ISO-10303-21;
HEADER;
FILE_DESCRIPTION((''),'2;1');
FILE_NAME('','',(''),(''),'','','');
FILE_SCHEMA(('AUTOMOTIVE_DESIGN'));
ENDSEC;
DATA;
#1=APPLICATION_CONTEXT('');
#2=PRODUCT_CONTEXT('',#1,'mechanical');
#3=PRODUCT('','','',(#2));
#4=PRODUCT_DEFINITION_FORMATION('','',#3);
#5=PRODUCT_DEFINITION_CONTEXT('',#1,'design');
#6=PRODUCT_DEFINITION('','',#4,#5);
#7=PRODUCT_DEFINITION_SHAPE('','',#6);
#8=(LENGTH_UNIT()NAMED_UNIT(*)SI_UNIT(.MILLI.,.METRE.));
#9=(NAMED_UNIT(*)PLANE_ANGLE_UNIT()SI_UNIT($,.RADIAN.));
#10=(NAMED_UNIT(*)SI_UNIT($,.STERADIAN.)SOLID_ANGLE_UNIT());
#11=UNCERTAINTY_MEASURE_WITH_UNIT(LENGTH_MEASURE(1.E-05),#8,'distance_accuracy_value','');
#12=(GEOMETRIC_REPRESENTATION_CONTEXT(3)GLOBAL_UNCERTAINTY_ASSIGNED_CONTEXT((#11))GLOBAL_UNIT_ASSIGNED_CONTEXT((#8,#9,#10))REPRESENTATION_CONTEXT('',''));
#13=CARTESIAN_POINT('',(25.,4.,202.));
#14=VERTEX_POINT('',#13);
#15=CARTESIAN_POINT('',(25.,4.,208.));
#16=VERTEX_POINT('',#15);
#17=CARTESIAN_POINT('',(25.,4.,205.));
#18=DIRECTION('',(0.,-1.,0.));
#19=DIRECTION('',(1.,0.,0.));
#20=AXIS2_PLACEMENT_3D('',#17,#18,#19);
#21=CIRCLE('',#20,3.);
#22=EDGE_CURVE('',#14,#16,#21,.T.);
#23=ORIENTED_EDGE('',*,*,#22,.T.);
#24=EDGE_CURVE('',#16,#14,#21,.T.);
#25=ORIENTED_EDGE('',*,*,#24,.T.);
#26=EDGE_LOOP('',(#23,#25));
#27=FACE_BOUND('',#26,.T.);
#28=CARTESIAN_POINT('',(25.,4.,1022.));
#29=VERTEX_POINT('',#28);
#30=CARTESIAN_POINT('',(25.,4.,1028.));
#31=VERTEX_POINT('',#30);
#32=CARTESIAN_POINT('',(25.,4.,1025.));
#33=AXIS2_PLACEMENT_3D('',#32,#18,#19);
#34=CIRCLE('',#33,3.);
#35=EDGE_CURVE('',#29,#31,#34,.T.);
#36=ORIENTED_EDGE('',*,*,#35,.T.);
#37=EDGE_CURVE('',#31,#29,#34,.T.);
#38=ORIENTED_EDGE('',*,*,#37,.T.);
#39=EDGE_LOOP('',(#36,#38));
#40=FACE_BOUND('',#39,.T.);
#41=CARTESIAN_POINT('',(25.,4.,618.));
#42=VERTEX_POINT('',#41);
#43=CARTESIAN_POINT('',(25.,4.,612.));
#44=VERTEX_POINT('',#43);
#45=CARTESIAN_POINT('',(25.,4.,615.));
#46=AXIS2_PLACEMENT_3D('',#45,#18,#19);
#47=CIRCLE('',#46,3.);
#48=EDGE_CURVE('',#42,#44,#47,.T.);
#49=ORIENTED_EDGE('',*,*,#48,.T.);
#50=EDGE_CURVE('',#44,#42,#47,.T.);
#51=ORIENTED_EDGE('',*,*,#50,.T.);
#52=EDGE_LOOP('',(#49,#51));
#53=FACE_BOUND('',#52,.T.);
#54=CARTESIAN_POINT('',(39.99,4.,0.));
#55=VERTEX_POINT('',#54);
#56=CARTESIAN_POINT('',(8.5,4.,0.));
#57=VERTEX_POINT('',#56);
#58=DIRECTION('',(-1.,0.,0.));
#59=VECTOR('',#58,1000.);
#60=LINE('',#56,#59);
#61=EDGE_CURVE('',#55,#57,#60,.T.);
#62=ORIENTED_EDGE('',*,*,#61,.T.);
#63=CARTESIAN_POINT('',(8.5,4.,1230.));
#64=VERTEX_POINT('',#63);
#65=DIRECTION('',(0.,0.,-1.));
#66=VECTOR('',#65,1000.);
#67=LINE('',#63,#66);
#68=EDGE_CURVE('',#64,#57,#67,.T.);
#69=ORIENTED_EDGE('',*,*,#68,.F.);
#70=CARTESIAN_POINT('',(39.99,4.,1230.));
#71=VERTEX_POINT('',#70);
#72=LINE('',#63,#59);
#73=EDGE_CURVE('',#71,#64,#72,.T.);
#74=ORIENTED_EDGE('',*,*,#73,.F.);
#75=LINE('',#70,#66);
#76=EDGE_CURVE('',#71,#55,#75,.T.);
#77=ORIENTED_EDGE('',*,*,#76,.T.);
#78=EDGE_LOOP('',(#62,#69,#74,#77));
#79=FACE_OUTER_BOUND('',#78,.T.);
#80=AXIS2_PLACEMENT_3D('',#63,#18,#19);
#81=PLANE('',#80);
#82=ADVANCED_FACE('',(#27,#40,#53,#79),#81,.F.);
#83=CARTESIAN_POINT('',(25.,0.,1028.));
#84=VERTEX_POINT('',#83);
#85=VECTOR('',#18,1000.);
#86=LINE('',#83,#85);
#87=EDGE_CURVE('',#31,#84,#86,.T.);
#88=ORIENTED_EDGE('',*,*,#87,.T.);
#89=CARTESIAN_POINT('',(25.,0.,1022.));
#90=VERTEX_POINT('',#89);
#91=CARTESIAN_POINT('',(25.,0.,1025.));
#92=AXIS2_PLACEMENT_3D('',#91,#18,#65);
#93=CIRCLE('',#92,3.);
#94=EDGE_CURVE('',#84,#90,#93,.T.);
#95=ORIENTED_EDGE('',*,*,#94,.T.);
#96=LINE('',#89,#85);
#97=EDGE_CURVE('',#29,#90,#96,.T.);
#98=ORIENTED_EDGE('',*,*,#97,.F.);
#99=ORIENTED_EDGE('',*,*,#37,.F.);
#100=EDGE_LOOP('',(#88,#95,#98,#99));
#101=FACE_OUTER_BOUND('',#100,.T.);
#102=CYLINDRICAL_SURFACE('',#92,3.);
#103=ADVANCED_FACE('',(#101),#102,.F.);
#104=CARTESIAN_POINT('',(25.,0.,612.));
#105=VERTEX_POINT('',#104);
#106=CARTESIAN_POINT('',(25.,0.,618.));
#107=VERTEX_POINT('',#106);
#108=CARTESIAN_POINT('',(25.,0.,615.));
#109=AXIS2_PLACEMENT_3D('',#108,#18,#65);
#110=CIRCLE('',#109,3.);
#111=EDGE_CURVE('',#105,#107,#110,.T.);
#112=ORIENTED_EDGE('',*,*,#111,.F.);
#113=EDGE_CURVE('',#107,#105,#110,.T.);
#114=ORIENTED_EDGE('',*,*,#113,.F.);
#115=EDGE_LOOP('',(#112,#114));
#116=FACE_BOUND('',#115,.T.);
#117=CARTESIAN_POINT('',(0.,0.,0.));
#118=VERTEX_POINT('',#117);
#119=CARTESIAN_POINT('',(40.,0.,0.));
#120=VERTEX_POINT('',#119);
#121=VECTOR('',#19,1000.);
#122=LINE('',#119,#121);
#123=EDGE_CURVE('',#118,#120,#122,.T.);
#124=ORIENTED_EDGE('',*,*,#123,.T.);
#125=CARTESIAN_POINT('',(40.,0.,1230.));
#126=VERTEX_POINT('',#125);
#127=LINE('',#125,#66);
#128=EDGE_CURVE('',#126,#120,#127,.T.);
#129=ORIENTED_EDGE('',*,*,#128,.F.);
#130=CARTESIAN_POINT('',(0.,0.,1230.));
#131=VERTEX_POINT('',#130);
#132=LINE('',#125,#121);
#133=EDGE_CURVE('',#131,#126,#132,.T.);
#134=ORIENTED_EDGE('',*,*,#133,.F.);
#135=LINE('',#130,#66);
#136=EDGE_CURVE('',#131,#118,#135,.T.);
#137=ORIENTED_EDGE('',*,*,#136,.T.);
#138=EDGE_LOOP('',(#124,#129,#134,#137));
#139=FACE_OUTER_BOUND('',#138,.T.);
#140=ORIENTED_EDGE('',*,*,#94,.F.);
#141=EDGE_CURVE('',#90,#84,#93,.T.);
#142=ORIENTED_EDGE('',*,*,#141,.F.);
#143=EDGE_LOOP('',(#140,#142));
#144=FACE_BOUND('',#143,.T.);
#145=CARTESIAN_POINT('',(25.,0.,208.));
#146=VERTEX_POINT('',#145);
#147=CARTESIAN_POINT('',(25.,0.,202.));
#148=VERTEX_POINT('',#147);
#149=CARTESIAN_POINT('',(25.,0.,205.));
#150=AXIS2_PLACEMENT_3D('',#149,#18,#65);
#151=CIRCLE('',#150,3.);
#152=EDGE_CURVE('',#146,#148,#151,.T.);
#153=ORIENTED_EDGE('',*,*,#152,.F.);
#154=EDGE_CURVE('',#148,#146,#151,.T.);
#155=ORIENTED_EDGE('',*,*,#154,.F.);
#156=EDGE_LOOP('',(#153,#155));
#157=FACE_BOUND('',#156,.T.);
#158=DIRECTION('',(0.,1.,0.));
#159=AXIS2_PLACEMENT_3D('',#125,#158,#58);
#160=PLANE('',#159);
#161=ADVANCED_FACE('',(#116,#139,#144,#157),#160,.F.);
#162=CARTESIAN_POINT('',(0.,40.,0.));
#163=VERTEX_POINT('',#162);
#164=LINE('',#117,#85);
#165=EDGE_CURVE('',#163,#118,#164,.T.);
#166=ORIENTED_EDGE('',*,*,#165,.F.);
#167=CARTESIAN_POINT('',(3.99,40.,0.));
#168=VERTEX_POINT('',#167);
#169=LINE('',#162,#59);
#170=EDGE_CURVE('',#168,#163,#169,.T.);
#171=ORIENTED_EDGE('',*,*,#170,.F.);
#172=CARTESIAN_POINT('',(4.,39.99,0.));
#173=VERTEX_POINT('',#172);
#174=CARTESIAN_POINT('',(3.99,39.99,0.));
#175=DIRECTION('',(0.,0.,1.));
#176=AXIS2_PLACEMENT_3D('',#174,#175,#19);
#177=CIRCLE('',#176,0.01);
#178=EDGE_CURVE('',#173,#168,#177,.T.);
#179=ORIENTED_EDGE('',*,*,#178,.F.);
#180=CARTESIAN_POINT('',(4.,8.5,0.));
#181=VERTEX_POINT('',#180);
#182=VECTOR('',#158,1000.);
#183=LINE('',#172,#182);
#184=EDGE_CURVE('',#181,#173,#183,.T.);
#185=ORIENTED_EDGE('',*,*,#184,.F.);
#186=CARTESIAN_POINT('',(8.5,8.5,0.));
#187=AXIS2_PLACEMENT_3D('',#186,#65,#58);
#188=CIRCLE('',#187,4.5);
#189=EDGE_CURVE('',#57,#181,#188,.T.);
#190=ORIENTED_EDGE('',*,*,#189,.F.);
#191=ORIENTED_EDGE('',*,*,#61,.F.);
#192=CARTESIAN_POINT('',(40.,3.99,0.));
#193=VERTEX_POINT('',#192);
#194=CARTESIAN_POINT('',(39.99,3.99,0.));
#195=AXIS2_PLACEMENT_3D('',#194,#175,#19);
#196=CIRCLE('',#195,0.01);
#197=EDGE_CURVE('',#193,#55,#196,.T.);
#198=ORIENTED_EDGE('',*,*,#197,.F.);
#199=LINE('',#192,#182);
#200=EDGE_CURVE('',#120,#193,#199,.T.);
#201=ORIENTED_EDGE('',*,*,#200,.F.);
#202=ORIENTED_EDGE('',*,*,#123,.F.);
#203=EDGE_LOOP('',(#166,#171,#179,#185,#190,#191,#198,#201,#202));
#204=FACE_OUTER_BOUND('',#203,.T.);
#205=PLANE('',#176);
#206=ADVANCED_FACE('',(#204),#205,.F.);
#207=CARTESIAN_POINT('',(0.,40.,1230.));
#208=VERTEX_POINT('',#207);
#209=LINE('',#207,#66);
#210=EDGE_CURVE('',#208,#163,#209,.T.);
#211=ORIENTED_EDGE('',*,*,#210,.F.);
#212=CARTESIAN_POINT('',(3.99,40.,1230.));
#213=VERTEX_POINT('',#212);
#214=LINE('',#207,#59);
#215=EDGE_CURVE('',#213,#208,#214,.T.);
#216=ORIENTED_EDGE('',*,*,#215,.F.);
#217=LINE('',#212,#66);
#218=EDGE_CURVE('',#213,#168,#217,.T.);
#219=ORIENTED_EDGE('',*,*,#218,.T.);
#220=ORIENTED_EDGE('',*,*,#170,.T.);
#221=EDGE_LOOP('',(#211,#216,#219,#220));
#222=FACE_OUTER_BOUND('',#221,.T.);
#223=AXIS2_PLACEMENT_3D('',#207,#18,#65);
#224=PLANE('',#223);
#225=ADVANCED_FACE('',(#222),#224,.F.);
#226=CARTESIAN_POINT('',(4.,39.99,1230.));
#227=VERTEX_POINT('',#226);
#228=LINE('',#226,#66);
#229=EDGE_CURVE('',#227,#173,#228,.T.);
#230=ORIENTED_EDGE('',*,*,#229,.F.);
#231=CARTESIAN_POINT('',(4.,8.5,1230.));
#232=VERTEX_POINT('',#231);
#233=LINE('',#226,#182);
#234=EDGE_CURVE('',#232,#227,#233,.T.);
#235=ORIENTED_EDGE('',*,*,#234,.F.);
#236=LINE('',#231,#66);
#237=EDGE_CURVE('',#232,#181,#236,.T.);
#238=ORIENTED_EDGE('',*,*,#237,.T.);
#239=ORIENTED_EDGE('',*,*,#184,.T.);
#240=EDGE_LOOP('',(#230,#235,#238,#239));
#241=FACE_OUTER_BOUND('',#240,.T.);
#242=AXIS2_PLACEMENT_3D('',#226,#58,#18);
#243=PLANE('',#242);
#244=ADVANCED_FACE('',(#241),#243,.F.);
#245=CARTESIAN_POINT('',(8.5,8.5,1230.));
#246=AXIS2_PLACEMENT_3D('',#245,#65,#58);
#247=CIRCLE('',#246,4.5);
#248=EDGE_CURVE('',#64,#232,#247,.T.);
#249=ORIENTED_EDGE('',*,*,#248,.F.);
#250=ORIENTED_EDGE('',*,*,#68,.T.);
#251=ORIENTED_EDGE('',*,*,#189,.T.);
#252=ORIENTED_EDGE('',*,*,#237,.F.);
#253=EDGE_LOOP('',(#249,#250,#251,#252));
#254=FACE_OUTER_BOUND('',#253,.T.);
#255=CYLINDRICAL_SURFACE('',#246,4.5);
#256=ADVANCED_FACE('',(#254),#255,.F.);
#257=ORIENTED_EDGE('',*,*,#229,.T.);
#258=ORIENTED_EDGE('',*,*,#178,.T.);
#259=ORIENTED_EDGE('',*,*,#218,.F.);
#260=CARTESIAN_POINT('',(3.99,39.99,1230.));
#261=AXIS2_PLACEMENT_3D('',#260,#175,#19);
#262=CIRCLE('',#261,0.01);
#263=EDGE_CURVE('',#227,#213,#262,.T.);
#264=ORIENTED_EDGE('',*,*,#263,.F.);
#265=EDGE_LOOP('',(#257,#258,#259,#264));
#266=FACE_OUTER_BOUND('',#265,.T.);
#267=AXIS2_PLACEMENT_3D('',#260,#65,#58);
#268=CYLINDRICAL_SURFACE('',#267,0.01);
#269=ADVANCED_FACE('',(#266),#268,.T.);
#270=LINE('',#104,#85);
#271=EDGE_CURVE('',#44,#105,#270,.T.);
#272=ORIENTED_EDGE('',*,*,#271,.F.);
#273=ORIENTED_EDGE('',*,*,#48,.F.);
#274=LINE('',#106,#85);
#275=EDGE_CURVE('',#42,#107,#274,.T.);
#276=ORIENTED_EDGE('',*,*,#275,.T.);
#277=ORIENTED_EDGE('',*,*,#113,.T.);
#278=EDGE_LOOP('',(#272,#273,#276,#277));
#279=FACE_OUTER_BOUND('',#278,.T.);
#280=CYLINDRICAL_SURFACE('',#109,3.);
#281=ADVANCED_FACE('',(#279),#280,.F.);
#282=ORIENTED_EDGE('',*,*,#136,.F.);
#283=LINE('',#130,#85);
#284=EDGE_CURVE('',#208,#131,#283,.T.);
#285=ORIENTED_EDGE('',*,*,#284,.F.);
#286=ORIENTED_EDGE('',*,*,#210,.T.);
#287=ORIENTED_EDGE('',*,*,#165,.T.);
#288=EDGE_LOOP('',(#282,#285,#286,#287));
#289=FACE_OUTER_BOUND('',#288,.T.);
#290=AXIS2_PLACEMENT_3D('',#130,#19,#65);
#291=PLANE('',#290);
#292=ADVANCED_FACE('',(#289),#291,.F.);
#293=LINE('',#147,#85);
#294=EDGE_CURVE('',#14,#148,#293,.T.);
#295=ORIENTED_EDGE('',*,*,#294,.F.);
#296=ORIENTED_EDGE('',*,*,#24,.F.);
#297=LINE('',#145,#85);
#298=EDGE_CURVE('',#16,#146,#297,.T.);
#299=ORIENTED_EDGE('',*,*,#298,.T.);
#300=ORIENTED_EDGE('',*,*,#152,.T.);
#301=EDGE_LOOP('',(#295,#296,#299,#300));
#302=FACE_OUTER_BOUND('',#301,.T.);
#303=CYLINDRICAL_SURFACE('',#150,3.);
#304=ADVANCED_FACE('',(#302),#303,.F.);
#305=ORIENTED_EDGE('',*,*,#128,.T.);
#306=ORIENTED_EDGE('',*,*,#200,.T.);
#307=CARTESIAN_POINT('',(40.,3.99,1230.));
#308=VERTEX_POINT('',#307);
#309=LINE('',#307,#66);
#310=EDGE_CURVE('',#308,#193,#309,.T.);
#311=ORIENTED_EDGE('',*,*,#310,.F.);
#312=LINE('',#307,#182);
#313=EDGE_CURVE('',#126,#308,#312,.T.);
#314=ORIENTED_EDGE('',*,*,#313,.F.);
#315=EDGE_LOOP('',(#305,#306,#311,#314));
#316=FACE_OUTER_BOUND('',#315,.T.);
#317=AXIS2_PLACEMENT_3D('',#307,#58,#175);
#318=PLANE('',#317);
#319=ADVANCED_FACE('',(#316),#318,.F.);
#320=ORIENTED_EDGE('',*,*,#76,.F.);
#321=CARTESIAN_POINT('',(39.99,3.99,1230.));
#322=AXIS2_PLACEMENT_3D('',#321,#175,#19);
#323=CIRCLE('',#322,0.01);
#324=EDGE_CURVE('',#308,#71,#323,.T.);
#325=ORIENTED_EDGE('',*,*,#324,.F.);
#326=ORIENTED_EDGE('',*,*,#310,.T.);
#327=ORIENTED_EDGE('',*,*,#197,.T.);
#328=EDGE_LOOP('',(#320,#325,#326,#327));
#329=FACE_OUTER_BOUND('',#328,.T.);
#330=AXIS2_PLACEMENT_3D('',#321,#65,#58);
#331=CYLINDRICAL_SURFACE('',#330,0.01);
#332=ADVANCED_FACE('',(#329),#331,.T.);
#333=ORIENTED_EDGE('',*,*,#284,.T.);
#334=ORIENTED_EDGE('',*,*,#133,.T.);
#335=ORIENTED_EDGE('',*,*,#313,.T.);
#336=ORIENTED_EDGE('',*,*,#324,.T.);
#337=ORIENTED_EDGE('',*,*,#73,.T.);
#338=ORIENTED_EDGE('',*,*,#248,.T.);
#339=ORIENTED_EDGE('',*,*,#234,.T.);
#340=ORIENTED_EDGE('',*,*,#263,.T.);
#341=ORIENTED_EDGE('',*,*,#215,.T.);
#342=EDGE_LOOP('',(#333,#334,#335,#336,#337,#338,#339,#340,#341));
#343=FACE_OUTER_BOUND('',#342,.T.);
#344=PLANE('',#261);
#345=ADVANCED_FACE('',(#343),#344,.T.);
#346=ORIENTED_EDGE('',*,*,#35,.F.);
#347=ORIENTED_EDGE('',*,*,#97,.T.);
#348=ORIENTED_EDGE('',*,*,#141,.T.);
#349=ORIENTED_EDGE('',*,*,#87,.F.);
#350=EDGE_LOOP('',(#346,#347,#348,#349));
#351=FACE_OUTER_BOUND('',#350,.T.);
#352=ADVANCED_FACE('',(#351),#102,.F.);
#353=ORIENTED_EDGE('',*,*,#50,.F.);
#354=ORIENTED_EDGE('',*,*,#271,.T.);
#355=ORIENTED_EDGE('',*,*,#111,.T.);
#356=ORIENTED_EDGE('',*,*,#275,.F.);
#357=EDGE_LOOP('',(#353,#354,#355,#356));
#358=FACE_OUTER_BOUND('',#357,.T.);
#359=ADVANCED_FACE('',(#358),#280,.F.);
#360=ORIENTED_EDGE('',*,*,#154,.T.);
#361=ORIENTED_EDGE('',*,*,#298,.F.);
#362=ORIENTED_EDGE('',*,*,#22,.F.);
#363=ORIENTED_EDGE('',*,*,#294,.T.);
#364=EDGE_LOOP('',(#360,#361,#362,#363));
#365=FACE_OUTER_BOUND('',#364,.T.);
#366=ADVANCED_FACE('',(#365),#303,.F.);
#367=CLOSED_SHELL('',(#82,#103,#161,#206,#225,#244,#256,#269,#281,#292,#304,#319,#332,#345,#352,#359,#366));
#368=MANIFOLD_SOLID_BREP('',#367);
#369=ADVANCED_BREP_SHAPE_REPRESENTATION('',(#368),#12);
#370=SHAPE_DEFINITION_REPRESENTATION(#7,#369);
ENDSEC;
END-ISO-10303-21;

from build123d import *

# Parameters (mm, degrees)
EXTRUDE_1_DEPTH        = 1230
HOLE_WIZARD_6_0_6_1_D  = 6
PATTERN_LINEAR_1_COUNT = 3
PATTERN_LINEAR_1_PITCH = 410


with BuildPart() as part:
    # 草图1 → 拉伸1 (new body)
    with BuildSketch(Plane.XY):
        with BuildLine():
            Line((0, 0), (0, 40))
            Line((0, 40), (3.99, 40))
            ThreePointArc((3.99, 40), (3.997071068, 39.997071068), (4, 39.99))
            Line((4, 39.99), (4, 8.5))
            ThreePointArc((4, 8.5), (5.318019485, 5.318019485), (8.5, 4))
            Line((8.5, 4), (39.99, 4))
            ThreePointArc((39.99, 4), (39.997071068, 3.997071068), (40, 3.99))
            Line((40, 3.99), (40, 0))
            Line((40, 0), (0, 0))
        make_face()
    extrude(amount=EXTRUDE_1_DEPTH)

    # Ø6.0 (6) 直径孔1 (through all)
    with Locations(Plane(origin=(0, 0, 0), x_dir=(-1, 0, 0), z_dir=(0, -1, 0))):
        with Locations((-25, -205)):
            hole_wizard_6_0_6_1 = Hole(HOLE_WIZARD_6_0_6_1_D / 2)

    # 阵列(线性)1: Ø6.0 (6) 直径孔1 ×3
    with Locations(*[(0, 0, i * PATTERN_LINEAR_1_PITCH) for i in range(1, PATTERN_LINEAR_1_COUNT)]):
        add(hole_wizard_6_0_6_1, mode=Mode.SUBTRACT)


solid = part.part
